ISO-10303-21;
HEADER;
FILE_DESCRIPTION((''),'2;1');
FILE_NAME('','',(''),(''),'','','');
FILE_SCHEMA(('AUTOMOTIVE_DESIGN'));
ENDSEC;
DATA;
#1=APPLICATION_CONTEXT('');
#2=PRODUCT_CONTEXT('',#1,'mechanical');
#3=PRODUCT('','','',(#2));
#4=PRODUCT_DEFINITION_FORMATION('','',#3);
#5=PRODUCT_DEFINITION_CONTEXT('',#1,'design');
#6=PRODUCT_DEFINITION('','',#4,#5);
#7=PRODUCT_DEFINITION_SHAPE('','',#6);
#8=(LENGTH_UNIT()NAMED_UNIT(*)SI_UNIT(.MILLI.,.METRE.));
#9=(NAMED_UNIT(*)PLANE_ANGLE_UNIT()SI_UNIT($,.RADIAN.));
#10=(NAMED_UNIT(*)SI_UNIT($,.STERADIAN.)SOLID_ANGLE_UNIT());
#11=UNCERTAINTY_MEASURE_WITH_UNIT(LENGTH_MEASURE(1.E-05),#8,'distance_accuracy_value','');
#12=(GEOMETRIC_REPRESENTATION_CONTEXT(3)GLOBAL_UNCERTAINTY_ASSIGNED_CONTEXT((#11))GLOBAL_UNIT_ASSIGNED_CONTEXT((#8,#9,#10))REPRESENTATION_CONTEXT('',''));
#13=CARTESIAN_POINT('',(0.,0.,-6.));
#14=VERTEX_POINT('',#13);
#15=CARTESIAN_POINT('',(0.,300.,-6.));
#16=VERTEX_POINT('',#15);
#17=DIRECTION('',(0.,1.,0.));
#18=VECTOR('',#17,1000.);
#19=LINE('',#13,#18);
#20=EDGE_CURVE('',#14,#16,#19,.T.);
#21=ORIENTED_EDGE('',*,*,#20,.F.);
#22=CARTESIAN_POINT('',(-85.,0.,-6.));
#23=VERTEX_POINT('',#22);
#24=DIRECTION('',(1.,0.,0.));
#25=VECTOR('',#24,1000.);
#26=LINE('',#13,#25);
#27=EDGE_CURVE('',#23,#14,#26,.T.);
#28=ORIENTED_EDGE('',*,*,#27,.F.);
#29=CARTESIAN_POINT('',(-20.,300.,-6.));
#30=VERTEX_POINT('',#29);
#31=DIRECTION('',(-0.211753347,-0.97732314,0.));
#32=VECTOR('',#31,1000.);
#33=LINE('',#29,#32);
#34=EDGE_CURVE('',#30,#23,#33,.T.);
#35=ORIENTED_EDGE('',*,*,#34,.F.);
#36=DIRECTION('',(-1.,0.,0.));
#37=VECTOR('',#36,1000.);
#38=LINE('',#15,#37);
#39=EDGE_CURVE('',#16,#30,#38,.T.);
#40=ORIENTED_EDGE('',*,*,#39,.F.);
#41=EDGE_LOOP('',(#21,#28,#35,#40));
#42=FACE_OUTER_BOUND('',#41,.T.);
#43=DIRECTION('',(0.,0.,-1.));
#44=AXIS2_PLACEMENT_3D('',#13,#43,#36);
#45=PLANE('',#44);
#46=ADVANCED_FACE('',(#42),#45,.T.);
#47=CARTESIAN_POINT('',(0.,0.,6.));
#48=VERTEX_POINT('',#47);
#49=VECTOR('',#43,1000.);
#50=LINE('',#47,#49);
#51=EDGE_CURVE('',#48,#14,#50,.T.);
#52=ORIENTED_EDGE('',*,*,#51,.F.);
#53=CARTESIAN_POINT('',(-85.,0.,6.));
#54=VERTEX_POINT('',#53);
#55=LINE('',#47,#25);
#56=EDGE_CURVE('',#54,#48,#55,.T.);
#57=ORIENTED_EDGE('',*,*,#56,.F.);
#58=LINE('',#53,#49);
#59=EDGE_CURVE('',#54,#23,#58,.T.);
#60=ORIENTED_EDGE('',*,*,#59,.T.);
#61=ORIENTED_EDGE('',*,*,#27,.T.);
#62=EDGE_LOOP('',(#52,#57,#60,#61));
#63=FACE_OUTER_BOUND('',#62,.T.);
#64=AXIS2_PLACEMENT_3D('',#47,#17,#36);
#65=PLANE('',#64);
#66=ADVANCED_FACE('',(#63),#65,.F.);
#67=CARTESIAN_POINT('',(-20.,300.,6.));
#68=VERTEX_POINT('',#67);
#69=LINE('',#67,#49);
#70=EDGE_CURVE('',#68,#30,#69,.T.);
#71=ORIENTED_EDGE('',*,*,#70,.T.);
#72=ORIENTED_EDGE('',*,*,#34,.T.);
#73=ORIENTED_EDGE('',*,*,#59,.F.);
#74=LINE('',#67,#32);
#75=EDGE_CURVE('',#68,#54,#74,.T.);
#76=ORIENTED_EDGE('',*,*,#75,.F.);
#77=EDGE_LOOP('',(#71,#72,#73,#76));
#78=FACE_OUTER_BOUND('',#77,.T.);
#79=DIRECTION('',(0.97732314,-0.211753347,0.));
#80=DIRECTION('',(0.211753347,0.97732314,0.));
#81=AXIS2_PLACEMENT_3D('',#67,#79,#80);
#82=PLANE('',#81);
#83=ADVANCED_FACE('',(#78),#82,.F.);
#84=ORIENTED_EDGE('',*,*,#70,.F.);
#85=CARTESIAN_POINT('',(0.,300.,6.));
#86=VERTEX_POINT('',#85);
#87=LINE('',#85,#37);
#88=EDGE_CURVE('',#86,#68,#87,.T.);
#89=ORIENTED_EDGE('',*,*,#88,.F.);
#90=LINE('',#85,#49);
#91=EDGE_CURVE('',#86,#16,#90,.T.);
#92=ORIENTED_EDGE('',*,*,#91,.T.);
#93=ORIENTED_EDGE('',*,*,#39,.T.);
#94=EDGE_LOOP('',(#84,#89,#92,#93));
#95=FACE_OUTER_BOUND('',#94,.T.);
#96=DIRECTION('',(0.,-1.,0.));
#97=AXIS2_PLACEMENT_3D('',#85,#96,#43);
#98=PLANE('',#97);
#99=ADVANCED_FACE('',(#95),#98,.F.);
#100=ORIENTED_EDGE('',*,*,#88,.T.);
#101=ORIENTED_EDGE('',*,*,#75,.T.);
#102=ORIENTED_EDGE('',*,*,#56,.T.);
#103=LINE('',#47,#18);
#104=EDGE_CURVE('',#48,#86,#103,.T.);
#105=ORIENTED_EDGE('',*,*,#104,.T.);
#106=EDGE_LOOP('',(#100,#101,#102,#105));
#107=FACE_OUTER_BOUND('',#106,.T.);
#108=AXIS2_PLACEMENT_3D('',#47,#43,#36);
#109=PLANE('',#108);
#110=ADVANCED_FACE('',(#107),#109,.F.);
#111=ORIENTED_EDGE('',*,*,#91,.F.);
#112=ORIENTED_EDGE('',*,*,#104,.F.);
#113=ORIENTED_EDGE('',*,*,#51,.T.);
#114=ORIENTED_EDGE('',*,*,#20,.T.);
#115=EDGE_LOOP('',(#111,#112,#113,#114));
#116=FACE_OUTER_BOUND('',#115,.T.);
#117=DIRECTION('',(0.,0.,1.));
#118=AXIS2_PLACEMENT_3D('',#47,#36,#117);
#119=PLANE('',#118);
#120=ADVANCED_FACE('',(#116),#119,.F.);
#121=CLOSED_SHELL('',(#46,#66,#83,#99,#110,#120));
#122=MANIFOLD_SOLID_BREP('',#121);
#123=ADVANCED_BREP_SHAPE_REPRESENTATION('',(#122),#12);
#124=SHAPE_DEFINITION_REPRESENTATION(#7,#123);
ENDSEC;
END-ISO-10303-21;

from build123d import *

# Parameters (mm, degrees)
EXTRUDE1_DEPTH = 6


with BuildPart() as part:
    # Sketch1 → Extrude1 (new, symmetric)
    with BuildSketch(Plane.XY):
        Polygon((0, 0), (0, 300), (-20, 300), (-85, 0), align=None)
    extrude(amount=EXTRUDE1_DEPTH, both=True)


solid = part.part
